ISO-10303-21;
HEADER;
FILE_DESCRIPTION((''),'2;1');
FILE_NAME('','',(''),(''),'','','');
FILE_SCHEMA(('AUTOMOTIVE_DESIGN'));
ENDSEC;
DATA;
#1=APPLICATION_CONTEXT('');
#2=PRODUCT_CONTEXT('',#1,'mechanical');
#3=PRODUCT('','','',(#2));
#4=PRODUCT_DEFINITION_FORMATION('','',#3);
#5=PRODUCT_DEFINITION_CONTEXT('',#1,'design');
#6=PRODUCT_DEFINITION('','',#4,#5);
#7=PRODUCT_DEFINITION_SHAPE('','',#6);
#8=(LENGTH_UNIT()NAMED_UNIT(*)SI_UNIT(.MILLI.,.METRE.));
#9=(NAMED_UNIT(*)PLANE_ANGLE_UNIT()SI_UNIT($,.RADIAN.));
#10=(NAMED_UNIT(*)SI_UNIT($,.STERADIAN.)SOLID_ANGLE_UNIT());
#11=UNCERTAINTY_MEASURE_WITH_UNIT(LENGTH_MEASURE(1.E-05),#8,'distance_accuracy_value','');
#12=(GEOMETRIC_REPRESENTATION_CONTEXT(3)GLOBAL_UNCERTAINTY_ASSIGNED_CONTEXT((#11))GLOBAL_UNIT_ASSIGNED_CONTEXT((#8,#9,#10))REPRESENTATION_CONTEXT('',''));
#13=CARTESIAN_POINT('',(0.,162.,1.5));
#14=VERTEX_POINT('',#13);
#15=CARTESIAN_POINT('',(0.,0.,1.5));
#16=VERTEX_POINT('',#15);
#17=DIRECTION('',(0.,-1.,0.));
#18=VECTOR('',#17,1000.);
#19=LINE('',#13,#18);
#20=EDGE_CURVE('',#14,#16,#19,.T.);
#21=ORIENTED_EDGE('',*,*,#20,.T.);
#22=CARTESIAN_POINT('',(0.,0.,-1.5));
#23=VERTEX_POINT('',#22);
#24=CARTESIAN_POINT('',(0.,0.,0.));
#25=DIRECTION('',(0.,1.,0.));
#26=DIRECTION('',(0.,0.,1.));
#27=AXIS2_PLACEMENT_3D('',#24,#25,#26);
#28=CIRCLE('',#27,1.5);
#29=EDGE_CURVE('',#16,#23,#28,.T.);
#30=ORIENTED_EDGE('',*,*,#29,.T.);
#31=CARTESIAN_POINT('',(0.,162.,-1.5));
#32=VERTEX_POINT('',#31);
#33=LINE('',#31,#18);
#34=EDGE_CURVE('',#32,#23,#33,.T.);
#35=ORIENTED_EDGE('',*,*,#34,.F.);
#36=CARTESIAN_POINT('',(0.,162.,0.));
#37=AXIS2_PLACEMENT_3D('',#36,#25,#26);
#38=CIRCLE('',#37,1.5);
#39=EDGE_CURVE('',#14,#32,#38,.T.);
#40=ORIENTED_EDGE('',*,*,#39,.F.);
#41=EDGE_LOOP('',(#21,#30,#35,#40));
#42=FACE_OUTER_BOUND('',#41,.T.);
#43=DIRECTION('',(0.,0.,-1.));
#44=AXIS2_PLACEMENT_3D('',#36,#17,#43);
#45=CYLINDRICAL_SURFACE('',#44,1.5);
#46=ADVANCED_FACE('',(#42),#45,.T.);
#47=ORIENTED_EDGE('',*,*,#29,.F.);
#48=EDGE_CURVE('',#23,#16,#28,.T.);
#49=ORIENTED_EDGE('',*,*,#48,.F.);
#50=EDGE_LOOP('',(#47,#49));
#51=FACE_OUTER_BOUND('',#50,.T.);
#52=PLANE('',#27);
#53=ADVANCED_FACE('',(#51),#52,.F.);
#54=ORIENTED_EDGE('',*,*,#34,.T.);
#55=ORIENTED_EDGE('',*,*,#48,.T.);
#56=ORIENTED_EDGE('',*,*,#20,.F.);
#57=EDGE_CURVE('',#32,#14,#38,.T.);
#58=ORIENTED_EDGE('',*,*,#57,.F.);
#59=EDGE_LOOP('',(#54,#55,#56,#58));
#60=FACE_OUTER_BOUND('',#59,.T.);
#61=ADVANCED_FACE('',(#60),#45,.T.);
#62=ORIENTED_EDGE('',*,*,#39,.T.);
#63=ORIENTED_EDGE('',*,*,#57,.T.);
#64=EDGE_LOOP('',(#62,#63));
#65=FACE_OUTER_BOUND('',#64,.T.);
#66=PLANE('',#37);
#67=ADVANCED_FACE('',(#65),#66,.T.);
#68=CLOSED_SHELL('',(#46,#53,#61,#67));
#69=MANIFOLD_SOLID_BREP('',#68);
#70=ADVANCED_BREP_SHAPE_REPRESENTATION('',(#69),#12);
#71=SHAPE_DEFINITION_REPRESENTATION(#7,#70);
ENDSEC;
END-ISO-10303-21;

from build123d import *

# Parameters (mm, degrees)
SKETCH1_R           = 1.5
BOSS_EXTRUDE1_DEPTH = 162


with BuildPart() as part:
    # Sketch1 → Boss-Extrude1 (new body)
    with BuildSketch(Plane(origin=(0, 0, 0), x_dir=(1, 0, 0), z_dir=(0, 1, 0))):
        with Locations(Location((0, 0, 0), (0, 0, 270))):
            Circle(SKETCH1_R)
    extrude(amount=BOSS_EXTRUDE1_DEPTH)


solid = part.part
